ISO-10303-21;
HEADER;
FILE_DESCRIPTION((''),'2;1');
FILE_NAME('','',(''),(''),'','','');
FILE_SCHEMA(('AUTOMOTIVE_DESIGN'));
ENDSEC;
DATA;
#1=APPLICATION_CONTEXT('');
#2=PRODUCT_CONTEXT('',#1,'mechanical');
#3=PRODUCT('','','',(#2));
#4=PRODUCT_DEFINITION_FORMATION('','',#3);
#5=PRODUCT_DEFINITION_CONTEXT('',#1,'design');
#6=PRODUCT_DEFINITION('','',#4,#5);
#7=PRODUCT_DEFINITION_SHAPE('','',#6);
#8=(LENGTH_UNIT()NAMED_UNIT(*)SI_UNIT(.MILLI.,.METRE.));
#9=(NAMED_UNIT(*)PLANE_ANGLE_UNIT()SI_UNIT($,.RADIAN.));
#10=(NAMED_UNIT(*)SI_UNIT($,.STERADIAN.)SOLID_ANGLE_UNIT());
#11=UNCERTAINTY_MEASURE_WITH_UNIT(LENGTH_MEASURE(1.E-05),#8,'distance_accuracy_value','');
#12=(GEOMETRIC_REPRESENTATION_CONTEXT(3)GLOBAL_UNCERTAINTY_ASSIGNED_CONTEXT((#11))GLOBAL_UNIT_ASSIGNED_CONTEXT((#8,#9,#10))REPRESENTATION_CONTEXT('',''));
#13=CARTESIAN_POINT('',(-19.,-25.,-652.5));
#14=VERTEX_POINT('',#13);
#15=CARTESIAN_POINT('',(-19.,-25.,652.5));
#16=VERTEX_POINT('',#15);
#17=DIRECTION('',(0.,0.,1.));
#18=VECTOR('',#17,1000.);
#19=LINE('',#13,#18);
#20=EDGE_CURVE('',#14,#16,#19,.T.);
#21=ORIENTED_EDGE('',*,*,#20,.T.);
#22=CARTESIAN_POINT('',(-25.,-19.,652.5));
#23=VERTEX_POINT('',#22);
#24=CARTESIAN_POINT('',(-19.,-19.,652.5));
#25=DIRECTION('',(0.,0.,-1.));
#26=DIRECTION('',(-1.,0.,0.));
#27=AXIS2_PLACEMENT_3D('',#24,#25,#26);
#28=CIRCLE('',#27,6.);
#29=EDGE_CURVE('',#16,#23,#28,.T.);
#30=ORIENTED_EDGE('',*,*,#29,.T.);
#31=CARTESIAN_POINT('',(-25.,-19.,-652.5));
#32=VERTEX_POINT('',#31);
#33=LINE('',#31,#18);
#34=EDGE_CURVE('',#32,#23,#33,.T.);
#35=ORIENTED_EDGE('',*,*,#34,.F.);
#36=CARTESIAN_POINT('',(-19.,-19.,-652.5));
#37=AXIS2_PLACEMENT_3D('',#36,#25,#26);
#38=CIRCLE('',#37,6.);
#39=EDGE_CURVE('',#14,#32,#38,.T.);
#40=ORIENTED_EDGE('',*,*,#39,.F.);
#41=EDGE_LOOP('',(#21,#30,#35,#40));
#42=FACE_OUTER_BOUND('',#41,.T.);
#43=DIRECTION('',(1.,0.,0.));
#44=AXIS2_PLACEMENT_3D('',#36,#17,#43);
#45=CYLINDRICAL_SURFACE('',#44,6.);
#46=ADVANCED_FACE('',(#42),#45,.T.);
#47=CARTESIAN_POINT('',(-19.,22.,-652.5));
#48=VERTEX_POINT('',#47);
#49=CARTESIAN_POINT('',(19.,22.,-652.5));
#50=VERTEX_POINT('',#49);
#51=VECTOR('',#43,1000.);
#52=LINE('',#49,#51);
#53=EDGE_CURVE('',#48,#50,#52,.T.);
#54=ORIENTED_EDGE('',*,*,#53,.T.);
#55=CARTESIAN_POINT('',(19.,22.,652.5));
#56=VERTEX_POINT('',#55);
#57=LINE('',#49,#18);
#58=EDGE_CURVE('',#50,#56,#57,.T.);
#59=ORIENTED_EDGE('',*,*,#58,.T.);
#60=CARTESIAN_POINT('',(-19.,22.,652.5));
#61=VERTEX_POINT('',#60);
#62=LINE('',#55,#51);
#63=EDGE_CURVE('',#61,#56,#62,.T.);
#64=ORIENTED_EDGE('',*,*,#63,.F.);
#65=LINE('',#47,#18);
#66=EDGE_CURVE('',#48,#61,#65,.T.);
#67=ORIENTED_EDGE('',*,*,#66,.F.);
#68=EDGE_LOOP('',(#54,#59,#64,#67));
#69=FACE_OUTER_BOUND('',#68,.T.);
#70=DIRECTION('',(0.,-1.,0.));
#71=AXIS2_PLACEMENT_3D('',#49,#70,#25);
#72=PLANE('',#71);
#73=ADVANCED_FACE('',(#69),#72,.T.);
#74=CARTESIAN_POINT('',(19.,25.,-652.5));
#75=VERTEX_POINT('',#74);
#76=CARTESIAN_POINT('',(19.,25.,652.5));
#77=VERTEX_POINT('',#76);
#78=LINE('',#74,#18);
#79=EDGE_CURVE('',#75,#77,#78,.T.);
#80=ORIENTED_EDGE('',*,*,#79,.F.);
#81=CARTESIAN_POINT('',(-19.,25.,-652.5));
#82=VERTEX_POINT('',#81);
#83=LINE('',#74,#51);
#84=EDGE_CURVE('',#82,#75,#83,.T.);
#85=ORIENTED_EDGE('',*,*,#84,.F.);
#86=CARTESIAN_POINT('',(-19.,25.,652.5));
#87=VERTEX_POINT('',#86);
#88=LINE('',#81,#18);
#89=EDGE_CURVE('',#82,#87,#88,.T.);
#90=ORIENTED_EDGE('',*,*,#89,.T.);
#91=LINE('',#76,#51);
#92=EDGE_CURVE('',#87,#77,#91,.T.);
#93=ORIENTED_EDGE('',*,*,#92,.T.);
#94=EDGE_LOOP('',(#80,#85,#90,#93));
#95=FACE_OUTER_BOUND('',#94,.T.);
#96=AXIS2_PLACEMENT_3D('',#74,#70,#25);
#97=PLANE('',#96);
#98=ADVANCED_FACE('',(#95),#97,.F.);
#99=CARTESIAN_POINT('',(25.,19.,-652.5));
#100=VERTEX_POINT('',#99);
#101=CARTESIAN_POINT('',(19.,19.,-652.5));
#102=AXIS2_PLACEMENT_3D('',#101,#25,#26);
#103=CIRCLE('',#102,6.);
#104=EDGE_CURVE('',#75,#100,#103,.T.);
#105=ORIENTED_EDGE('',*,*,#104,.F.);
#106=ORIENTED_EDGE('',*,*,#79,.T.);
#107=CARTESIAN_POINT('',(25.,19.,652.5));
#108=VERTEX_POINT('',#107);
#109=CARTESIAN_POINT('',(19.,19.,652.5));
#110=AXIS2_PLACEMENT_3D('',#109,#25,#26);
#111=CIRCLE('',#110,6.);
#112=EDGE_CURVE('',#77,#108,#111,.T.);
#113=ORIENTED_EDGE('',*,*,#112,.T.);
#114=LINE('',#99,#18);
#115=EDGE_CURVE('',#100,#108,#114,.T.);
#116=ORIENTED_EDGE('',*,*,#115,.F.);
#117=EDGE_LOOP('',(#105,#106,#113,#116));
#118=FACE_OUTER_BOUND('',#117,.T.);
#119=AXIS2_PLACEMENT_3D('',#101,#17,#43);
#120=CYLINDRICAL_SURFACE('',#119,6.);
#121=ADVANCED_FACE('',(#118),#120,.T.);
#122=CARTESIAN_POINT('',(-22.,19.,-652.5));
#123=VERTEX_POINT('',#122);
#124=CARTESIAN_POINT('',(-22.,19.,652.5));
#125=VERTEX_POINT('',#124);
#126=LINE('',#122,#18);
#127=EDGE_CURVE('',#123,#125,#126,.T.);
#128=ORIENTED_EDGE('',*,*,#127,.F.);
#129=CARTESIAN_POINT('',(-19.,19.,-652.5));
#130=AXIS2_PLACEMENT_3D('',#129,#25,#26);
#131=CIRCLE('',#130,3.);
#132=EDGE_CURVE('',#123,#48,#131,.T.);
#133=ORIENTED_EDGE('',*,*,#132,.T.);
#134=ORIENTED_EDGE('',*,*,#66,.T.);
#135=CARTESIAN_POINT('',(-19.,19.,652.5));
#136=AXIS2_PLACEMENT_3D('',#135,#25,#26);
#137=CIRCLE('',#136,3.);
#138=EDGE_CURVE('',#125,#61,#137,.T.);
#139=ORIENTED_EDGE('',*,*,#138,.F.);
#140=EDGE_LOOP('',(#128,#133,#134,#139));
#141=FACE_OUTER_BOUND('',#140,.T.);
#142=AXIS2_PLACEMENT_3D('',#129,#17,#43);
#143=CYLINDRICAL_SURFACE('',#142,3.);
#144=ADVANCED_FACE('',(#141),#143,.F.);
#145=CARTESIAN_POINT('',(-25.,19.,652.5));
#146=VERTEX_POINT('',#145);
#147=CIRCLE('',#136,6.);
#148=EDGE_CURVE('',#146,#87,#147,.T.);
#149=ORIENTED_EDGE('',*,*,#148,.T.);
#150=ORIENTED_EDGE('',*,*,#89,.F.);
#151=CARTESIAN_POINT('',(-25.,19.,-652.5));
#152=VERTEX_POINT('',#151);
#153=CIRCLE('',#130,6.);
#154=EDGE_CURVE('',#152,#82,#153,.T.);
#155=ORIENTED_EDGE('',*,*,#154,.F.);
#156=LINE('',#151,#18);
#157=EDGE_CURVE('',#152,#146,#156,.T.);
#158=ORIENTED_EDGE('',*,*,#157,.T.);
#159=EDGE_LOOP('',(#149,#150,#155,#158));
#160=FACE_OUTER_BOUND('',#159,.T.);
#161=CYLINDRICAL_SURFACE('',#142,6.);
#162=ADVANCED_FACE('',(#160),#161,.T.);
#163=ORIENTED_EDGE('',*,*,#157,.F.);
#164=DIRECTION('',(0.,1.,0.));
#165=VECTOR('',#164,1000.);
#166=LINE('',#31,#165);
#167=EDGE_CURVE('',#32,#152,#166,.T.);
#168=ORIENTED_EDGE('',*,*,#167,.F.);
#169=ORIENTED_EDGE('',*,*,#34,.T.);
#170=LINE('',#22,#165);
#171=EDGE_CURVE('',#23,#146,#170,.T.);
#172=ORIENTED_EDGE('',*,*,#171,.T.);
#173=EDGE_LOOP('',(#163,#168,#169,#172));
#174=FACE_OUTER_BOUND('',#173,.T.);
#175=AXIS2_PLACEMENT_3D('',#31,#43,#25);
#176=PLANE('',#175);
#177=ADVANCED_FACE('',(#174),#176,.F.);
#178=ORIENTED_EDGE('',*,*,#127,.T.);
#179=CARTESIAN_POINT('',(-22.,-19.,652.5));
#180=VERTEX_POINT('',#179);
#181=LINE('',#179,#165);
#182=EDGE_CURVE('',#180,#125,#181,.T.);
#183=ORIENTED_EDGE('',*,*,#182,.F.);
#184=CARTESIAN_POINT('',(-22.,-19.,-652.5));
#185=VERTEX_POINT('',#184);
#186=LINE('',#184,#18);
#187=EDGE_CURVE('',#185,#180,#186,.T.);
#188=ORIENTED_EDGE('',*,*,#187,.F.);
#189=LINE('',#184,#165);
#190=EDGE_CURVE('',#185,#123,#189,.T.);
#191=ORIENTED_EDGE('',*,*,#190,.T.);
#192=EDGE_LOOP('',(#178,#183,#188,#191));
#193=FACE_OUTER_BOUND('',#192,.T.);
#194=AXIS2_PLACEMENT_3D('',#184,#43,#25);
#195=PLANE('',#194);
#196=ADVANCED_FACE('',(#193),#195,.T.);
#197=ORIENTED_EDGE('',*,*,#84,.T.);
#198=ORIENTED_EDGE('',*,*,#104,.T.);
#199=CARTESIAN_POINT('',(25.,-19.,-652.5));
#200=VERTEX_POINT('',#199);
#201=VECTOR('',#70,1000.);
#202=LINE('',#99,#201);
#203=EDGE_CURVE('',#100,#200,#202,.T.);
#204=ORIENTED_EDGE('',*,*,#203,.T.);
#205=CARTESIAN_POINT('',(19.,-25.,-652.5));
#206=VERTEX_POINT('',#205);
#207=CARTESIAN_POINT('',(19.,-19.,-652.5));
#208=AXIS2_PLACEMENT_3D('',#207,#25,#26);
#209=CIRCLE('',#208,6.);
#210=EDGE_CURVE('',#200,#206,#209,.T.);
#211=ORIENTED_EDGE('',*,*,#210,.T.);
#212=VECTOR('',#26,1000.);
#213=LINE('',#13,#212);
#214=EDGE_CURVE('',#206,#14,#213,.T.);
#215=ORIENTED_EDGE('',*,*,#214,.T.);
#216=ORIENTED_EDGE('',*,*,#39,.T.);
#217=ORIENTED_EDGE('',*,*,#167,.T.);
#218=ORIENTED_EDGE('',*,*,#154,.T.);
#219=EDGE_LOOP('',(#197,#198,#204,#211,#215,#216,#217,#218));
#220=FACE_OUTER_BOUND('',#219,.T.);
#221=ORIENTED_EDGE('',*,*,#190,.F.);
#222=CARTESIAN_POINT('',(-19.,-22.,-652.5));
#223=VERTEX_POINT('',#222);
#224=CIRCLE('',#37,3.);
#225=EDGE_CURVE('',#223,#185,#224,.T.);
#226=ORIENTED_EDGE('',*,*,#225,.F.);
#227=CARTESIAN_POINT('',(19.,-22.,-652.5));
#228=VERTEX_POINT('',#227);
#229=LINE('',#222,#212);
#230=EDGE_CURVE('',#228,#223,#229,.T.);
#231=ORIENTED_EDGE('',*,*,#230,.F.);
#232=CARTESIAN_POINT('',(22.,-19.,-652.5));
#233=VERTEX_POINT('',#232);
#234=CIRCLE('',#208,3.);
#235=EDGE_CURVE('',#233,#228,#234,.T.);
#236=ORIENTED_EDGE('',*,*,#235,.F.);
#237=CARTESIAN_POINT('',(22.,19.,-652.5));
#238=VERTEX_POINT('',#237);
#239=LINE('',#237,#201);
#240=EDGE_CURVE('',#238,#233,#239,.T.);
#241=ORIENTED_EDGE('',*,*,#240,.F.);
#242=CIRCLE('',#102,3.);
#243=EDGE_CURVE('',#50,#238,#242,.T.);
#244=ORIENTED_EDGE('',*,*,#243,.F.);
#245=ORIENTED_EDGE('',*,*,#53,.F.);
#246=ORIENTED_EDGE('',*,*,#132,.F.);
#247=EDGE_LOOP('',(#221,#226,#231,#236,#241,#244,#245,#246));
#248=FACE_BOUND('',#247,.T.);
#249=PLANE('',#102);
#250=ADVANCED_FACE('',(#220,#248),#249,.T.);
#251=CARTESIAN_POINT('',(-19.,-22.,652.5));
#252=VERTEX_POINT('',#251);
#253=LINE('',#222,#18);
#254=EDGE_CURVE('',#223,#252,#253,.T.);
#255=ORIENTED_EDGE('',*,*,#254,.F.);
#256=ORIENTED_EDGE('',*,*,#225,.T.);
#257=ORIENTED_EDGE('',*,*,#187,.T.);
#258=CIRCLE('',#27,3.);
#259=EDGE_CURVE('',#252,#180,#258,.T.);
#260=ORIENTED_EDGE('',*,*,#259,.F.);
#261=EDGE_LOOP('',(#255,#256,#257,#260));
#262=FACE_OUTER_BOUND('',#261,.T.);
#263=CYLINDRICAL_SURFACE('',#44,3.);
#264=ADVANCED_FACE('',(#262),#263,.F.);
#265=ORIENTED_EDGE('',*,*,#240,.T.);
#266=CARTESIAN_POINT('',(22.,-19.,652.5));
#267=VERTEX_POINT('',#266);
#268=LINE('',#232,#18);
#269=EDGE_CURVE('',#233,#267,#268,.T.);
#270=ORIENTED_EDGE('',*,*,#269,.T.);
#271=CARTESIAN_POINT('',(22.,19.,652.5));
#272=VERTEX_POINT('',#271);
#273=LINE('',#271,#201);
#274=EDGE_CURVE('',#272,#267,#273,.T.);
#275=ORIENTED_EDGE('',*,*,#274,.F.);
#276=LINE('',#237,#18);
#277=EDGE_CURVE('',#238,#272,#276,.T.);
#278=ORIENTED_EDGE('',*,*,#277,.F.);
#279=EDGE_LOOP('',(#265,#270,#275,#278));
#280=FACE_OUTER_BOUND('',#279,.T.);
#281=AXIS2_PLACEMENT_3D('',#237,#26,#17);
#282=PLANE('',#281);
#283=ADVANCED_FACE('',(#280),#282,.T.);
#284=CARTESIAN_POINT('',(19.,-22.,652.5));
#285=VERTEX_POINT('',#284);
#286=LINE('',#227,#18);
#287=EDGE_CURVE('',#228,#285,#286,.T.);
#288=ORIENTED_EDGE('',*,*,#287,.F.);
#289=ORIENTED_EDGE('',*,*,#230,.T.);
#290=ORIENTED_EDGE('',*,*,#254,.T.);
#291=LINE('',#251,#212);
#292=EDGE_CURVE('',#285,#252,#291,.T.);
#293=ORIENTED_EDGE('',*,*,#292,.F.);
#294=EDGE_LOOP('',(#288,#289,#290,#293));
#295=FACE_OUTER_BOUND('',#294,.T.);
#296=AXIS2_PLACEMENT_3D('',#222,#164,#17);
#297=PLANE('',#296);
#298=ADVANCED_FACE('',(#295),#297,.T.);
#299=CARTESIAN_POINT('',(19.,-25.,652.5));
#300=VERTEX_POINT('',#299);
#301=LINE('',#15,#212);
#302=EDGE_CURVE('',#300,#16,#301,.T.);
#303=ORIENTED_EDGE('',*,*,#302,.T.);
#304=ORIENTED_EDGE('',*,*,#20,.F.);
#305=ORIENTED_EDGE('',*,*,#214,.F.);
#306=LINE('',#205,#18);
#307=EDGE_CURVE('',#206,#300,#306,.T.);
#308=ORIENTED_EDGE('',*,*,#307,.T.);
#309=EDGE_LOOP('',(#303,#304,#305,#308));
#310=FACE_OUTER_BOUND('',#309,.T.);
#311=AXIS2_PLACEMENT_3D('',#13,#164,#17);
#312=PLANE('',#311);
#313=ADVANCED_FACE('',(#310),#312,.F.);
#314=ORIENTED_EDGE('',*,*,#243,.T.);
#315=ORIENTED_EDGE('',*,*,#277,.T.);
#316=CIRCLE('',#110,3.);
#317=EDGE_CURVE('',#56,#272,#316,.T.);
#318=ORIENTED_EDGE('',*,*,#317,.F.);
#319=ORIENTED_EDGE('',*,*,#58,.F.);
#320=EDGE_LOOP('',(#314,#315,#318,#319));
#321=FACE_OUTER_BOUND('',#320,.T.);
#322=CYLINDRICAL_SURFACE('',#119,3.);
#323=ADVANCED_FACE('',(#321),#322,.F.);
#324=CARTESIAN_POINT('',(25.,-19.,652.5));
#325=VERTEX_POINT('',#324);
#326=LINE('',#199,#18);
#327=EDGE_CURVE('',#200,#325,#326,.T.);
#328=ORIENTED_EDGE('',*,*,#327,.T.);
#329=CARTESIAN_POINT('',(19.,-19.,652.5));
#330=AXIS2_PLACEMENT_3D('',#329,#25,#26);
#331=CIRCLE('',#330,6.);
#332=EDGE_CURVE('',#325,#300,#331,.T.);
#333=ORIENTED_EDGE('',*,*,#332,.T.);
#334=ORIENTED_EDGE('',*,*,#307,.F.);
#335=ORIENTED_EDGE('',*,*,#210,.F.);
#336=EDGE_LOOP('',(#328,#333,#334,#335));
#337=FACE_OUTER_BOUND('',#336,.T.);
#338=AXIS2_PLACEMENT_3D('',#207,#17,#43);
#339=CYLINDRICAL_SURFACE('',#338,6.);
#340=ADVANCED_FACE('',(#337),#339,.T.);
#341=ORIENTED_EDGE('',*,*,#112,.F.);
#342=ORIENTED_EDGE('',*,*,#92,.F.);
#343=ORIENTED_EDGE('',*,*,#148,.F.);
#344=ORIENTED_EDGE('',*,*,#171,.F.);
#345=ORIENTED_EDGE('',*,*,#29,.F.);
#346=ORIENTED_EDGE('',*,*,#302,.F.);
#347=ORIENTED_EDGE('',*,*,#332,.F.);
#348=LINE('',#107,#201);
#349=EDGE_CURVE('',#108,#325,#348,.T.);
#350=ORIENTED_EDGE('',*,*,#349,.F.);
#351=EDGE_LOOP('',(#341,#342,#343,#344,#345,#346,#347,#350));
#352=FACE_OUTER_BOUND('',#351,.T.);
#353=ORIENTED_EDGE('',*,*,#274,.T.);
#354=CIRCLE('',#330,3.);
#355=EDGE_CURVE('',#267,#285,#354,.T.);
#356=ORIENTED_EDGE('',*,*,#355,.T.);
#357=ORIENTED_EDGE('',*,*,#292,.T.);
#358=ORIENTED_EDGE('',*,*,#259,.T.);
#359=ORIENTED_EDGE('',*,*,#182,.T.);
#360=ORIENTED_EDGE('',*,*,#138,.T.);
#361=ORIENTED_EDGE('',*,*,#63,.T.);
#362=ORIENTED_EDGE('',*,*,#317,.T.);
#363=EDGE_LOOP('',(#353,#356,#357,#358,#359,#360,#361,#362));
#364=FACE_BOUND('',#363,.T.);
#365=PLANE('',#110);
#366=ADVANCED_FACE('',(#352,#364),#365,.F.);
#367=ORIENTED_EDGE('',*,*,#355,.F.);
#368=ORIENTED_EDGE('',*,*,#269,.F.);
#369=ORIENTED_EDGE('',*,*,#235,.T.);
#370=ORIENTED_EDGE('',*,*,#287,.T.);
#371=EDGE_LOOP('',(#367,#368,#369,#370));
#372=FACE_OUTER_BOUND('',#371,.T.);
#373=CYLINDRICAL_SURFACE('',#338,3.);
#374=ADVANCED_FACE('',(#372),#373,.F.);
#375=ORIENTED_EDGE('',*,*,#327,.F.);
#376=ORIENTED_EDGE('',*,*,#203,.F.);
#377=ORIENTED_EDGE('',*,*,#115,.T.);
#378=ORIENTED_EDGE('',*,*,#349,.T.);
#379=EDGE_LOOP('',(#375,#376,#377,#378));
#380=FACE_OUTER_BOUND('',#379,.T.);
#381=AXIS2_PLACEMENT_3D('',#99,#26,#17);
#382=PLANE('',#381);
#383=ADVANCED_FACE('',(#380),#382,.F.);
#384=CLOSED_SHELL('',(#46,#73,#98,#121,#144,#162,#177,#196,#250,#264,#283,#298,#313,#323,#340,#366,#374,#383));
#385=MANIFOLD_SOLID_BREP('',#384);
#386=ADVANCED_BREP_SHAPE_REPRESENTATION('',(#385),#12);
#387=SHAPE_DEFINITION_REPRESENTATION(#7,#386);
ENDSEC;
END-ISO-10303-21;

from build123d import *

# Parameters (mm, degrees)
GB_6728_1986_050_X_50_X_3_1_DEPTH = 1305


with BuildPart() as part:
    # Sketch1 → Gb／6728-1986方形空心型钢 050 X 50 X 3(1) (new body)
    with BuildSketch(Plane.YX.offset(-652.5)):
        with BuildLine():
            Line((-19, -25), (19, -25))
            ThreePointArc((19, -25), (23.242640687, -23.242640687), (25, -19))
            Line((25, -19), (25, 19))
            ThreePointArc((25, 19), (23.242640687, 23.242640687), (19, 25))
            Line((19, 25), (-19, 25))
            ThreePointArc((-19, 25), (-23.242640687, 23.242640687), (-25, 19))
            Line((-25, 19), (-25, -19))
            ThreePointArc((-25, -19), (-23.242640687, -23.242640687), (-19, -25))
        make_face()
        with BuildLine():
            Line((-19, -22), (19, -22))
            ThreePointArc((19, -22), (21.121320344, -21.121320344), (22, -19))
            Line((22, -19), (22, 19))
            ThreePointArc((22, 19), (21.121320344, 21.121320344), (19, 22))
            Line((19, 22), (-19, 22))
            ThreePointArc((-19, 22), (-21.121320344, 21.121320344), (-22, 19))
            Line((-22, 19), (-22, -19))
            ThreePointArc((-22, -19), (-21.121320344, -21.121320344), (-19, -22))
        make_face(mode=Mode.SUBTRACT)
    extrude(amount=GB_6728_1986_050_X_50_X_3_1_DEPTH)


solid = part.part
